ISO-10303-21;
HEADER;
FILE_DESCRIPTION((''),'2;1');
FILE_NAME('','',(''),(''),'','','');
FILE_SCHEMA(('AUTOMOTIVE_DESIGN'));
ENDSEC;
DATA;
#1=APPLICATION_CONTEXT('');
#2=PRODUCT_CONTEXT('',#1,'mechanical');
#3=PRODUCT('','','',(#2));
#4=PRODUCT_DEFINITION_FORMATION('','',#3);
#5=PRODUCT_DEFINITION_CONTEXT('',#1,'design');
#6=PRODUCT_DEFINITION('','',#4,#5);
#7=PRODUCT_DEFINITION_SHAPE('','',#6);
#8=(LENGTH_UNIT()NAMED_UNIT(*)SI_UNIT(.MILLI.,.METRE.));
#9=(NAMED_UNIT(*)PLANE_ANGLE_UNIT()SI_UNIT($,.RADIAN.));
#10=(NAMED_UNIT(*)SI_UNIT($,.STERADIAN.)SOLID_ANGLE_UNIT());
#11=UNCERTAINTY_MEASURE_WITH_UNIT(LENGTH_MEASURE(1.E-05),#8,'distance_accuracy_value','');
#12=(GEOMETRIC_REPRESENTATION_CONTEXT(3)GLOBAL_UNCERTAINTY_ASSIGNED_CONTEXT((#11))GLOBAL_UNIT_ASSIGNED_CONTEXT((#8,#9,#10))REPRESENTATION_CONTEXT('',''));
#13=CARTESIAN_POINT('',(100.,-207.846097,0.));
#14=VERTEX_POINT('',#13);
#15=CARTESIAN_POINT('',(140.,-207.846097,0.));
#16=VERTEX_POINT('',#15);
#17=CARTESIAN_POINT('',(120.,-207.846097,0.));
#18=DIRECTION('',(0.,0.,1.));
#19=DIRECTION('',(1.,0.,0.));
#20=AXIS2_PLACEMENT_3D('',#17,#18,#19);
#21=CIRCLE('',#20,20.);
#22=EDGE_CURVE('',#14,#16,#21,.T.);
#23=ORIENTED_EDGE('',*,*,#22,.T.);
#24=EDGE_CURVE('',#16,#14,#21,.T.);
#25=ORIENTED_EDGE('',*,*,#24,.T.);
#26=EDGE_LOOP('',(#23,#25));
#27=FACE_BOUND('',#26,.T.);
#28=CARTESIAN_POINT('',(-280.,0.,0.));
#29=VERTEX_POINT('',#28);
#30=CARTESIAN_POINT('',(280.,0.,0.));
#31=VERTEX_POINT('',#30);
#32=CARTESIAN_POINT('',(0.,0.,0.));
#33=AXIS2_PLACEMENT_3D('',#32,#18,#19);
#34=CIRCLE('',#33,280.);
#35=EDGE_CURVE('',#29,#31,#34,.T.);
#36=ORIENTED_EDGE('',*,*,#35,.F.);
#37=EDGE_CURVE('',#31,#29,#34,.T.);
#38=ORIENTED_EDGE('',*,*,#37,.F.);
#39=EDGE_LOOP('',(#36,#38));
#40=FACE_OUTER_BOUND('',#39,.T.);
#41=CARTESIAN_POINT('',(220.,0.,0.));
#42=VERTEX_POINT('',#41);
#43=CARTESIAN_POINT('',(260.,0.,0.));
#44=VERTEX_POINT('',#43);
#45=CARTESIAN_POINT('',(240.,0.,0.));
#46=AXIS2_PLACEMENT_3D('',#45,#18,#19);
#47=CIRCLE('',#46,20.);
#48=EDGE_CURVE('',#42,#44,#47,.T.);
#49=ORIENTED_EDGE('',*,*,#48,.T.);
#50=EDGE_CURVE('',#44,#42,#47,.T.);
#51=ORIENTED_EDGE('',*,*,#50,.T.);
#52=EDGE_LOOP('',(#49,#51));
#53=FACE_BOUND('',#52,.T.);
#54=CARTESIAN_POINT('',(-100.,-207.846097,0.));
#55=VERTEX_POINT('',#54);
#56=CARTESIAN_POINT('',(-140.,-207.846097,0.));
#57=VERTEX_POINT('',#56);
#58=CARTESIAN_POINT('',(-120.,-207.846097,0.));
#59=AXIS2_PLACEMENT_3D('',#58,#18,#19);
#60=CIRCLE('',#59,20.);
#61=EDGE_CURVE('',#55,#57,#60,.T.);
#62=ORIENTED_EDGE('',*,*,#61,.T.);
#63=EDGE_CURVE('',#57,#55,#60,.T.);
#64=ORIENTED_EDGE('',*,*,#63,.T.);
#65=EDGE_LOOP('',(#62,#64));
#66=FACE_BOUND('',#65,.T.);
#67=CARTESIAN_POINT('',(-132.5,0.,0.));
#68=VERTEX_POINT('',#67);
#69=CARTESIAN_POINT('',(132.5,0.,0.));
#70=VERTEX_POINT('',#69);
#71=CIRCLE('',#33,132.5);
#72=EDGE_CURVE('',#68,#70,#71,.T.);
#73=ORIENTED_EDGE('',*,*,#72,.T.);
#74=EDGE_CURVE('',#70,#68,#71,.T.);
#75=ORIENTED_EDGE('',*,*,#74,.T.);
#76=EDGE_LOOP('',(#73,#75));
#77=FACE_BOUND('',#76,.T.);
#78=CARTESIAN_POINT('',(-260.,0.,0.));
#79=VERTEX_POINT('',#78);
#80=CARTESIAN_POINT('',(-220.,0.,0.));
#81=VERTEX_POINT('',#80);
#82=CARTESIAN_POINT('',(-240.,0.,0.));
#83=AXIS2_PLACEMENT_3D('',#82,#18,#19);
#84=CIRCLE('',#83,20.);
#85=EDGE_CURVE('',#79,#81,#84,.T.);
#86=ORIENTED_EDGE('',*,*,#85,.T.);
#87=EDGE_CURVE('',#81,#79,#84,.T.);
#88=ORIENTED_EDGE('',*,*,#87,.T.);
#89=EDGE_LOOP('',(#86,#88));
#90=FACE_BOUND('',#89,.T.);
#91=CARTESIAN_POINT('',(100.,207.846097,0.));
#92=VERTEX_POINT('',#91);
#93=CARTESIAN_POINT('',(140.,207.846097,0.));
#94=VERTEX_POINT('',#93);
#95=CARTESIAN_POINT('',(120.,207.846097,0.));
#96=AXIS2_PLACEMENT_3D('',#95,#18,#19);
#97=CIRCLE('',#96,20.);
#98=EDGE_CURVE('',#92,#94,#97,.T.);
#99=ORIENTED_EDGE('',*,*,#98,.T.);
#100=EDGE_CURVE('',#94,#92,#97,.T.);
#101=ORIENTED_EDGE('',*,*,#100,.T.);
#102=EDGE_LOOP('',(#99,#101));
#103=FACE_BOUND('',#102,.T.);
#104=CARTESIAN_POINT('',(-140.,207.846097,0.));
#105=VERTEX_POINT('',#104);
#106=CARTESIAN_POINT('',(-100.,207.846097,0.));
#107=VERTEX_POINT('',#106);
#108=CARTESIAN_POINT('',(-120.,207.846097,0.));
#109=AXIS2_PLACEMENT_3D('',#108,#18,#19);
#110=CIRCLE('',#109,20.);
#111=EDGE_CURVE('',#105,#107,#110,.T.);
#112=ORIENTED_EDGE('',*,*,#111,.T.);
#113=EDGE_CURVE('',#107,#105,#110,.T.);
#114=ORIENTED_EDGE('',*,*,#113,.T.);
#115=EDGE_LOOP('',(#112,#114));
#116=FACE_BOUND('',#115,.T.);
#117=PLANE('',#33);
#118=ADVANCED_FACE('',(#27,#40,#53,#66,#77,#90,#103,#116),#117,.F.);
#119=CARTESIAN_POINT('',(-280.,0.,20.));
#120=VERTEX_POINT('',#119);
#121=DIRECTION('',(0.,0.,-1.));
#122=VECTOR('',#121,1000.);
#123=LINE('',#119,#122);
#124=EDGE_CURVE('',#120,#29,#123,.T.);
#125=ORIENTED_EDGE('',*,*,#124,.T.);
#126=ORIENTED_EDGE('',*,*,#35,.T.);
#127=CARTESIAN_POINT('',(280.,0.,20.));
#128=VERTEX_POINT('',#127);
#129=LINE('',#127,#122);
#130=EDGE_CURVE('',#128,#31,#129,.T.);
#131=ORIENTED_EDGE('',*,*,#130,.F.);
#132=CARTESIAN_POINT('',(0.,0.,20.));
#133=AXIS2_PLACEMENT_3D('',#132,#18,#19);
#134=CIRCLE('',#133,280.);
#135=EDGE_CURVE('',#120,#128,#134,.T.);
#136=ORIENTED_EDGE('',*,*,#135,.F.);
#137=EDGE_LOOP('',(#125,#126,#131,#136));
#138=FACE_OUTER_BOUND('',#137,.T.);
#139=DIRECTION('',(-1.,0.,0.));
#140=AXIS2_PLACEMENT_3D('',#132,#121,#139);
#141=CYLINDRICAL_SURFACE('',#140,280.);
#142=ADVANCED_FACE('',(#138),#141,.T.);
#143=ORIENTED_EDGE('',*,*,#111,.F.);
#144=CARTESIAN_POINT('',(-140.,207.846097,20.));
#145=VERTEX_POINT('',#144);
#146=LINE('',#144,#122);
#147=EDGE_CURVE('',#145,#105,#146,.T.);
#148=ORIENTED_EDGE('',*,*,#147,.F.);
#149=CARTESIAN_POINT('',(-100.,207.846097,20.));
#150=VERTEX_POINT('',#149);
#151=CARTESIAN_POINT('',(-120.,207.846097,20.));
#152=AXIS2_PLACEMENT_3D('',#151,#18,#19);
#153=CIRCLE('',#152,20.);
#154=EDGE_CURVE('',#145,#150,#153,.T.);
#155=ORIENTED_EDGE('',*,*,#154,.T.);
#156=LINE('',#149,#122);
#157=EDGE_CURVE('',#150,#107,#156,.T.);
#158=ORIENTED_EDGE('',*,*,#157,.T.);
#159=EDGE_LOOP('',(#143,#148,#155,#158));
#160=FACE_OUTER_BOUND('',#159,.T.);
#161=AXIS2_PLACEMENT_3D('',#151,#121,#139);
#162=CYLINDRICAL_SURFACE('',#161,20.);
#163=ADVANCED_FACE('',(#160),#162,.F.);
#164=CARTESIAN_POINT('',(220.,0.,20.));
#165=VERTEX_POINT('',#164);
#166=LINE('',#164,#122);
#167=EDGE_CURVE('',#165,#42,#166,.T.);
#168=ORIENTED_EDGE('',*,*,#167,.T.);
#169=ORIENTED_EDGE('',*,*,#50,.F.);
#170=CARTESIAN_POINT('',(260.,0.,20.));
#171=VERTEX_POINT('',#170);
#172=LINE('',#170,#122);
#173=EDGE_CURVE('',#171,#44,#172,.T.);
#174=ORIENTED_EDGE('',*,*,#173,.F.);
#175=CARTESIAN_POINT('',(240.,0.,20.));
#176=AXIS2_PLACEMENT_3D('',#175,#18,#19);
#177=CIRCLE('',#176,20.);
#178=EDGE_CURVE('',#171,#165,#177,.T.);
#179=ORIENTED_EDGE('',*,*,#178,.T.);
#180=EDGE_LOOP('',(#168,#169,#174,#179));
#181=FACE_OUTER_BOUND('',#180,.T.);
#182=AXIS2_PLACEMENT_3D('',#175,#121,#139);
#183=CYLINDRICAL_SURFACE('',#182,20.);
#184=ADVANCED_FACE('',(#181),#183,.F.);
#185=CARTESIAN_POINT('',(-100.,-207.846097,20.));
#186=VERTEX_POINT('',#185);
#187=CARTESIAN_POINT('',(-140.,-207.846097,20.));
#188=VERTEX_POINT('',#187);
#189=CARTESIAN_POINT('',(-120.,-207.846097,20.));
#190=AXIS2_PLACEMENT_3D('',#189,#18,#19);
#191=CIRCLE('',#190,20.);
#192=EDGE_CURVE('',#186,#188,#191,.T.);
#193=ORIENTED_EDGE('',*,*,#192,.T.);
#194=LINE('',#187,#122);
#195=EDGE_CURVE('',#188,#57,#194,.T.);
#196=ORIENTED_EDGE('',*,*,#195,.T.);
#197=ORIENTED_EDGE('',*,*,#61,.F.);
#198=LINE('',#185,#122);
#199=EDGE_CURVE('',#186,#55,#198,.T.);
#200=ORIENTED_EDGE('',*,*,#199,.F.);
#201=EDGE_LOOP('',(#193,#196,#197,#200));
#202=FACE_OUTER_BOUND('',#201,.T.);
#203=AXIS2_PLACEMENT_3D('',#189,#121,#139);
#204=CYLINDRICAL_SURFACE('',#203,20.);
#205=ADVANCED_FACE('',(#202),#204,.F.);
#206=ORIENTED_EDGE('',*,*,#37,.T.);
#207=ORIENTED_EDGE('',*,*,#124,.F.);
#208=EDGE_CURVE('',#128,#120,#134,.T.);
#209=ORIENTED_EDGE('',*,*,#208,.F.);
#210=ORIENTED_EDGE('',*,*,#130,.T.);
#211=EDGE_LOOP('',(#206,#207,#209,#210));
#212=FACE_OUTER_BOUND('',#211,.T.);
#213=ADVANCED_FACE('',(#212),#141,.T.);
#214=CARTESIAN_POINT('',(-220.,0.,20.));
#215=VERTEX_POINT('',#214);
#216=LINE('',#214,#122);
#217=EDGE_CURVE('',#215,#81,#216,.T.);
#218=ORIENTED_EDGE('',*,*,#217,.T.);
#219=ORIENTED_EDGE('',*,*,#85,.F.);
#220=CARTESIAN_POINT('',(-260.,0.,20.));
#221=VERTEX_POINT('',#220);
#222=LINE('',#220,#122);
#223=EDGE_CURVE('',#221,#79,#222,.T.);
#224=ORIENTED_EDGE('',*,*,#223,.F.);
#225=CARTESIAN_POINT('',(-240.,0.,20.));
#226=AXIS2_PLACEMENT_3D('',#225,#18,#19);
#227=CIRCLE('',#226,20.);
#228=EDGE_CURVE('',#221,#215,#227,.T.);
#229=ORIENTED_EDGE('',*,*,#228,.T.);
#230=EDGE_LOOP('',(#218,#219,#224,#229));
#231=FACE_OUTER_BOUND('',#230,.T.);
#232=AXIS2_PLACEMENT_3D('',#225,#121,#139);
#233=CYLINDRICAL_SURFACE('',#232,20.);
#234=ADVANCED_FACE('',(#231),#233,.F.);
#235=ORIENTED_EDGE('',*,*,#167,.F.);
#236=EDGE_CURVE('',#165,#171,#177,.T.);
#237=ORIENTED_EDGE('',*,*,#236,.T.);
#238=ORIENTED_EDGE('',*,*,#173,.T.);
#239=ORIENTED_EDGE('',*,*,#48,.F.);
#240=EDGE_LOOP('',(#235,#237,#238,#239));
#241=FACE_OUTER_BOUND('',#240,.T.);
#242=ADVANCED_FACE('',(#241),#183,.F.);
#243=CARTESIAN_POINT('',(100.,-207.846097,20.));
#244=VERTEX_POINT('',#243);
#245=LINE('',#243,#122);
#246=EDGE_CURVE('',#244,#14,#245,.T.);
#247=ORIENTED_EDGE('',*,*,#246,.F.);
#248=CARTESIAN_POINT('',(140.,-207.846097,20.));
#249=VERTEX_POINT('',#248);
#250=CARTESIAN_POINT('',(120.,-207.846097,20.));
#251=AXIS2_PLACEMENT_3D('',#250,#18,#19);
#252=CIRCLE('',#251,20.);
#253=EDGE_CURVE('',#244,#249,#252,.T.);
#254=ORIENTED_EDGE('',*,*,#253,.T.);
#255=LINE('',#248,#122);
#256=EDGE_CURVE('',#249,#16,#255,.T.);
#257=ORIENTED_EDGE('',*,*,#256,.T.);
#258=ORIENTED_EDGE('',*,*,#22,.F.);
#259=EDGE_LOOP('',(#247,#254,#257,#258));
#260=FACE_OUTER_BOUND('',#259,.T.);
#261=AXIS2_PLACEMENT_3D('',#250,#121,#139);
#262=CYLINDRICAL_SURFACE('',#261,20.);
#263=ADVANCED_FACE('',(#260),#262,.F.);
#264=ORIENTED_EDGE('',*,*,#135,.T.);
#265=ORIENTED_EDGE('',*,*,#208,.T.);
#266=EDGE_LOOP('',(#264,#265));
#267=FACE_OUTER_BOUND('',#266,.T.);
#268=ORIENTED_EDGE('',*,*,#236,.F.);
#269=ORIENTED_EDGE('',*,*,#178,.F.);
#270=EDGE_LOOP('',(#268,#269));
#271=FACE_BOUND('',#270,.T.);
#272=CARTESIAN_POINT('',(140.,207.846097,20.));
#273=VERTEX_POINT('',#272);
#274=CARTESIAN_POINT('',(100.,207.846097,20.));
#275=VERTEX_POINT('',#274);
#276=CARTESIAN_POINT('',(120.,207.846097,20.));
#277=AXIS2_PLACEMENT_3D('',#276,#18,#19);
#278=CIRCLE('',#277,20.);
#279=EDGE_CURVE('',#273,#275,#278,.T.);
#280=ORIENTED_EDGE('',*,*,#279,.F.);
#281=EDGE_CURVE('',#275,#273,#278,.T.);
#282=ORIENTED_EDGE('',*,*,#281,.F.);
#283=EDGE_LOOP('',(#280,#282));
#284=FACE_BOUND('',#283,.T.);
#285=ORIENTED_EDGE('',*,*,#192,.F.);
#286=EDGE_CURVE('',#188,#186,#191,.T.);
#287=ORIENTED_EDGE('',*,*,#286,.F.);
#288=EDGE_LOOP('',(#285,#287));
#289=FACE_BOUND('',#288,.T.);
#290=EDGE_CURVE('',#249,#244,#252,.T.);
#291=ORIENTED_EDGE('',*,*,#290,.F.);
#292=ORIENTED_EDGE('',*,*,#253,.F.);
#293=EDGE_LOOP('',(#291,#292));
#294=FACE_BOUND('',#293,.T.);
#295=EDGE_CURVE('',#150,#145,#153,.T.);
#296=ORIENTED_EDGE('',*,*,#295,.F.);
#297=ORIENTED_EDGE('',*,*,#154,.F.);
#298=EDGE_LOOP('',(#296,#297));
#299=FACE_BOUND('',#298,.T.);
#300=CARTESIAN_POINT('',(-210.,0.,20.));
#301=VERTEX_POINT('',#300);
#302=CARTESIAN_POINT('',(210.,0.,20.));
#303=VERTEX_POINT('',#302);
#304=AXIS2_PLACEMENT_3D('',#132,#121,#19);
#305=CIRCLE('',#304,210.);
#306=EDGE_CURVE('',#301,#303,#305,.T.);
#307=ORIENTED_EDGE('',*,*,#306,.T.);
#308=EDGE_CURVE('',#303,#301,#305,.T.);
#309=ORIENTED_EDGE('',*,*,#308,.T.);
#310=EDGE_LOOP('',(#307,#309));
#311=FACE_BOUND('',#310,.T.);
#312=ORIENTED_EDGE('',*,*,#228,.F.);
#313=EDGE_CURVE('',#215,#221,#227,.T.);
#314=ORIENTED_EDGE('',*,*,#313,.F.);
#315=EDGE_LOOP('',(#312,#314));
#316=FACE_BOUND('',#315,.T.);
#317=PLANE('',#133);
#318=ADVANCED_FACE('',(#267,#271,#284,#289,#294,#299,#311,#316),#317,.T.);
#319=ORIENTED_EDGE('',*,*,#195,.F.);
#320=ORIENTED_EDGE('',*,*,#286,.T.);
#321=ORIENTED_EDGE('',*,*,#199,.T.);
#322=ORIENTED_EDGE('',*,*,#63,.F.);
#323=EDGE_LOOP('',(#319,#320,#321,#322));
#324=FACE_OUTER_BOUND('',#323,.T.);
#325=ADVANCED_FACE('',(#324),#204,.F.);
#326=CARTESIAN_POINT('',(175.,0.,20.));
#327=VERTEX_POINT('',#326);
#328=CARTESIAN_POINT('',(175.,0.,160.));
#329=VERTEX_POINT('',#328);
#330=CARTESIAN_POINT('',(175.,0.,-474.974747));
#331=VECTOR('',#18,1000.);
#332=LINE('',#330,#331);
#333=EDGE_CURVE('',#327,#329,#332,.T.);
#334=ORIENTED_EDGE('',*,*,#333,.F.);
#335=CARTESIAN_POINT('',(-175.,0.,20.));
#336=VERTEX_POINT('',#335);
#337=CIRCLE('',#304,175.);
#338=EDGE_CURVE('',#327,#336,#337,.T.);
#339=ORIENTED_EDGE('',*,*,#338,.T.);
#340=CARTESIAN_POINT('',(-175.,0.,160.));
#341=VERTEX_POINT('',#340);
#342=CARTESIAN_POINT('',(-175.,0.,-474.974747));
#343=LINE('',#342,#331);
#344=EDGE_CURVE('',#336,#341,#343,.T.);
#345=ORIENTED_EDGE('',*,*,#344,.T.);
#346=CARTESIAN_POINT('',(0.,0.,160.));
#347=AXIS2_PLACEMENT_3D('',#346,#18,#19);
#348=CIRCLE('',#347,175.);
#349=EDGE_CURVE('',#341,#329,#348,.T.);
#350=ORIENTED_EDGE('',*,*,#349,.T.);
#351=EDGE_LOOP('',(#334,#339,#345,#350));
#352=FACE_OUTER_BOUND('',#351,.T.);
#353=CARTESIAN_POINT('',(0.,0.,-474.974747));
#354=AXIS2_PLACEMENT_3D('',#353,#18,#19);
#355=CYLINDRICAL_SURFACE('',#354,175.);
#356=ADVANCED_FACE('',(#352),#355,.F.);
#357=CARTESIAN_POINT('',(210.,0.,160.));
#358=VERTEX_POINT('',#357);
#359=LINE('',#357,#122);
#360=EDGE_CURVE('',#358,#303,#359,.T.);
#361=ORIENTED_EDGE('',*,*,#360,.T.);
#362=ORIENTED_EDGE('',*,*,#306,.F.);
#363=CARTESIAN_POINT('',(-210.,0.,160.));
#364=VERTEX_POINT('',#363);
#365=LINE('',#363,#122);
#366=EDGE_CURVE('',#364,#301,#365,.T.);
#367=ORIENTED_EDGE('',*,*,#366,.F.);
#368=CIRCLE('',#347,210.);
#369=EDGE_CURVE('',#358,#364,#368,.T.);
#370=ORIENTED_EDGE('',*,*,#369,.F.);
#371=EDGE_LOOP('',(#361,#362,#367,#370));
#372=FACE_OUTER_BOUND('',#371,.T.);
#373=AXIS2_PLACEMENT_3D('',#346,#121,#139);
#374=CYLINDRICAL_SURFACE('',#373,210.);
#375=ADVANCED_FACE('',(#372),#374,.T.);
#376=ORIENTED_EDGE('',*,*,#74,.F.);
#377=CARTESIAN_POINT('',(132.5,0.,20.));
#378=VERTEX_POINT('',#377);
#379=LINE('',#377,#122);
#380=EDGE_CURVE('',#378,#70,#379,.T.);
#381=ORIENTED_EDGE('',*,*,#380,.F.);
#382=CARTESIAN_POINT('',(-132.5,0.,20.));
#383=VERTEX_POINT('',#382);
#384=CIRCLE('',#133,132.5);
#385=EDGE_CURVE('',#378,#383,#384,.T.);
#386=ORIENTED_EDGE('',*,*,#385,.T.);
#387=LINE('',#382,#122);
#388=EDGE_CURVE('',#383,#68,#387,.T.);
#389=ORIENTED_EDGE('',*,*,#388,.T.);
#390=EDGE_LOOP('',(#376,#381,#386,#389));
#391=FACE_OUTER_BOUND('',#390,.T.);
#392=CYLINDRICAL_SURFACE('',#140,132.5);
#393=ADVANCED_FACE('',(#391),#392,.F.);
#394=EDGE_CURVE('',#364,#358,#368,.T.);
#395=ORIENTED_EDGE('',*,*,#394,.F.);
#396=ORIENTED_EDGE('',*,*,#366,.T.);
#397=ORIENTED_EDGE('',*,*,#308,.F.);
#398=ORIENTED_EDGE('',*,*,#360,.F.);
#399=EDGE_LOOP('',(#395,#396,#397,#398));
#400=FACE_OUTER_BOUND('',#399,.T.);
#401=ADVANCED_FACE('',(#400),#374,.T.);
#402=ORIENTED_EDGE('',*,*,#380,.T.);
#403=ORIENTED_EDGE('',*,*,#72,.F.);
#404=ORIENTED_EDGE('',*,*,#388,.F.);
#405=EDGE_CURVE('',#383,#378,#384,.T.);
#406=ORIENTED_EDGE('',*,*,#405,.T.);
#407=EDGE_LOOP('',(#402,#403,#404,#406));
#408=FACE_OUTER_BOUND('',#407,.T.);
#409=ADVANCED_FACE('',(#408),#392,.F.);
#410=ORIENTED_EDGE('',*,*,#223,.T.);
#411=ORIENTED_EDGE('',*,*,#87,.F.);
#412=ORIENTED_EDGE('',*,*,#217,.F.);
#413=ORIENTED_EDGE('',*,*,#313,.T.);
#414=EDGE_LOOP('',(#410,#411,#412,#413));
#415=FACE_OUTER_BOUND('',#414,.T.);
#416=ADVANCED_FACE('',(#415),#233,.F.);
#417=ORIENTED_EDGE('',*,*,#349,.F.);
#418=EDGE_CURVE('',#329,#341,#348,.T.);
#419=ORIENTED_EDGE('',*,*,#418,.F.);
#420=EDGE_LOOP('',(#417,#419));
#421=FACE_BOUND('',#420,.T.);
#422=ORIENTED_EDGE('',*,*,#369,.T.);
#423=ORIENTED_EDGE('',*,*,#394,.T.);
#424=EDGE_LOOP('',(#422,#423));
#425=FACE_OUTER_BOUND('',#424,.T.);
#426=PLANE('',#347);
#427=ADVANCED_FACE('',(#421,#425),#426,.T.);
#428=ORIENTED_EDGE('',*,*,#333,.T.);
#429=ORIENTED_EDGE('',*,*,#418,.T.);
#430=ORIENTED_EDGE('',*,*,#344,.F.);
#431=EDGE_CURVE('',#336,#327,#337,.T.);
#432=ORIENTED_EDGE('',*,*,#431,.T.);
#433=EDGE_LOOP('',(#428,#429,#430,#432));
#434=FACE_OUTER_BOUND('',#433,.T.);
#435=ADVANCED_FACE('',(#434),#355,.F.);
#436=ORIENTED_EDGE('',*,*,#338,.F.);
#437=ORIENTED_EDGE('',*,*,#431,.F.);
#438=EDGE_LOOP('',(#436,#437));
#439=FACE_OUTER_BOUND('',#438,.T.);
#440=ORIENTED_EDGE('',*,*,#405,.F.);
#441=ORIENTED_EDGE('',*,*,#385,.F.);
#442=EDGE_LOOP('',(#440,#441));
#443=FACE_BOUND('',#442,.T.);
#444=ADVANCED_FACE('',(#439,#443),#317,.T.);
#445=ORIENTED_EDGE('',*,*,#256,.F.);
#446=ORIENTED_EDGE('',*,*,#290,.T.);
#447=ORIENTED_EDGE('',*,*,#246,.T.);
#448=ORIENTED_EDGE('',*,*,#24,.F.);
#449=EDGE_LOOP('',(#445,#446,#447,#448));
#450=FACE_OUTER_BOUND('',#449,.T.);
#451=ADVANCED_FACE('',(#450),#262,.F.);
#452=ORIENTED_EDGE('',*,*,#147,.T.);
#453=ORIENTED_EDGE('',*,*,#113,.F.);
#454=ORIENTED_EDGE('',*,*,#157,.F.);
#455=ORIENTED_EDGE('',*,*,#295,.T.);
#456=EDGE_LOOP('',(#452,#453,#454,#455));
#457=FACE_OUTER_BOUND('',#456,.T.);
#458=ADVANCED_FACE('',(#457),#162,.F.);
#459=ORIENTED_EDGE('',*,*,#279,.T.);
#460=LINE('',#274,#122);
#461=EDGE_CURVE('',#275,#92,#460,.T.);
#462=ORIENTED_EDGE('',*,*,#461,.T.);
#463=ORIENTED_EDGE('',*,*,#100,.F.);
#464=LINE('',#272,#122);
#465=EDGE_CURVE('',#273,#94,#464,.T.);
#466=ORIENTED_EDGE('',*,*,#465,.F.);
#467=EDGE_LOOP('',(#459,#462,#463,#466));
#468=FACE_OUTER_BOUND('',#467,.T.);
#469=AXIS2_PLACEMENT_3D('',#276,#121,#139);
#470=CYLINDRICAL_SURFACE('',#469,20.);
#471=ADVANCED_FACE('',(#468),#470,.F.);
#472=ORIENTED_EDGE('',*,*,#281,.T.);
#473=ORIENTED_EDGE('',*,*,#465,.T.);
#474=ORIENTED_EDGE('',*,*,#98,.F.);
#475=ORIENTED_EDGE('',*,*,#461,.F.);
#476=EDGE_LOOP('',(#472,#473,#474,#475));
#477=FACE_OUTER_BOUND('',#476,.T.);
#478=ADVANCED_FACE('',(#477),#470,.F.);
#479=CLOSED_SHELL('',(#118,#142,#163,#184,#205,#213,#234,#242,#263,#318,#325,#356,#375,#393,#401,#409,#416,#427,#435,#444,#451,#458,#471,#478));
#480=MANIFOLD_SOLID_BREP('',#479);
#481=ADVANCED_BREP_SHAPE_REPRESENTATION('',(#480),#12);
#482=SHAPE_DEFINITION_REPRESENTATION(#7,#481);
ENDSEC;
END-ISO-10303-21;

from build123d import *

# Parameters (mm, degrees)
SKETCH_1_R          = 280
EXTRUDE_1_DEPTH     = 20
SKETCH_2_R          = 210
EXTRUDE_2_DEPTH     = 160
SKETCH_3_R          = 175
CUT_EXTRUDE_1_DEPTH = 140
SKETCH_4_R          = 20
CUT_EXTRUDE_3_DEPTH = 20
SKETCH_5_R          = 132.5
CUT_EXTRUDE_4_DEPTH = 20


with BuildPart() as part:
    # 草图1 → 凸台-拉伸1 (new body)
    with BuildSketch(Plane.XY):
        Circle(SKETCH_1_R)
    extrude(amount=EXTRUDE_1_DEPTH)

    # 草图2 → 凸台-拉伸2 (add)
    with BuildSketch(Plane.XY):
        Circle(SKETCH_2_R)
    extrude(amount=EXTRUDE_2_DEPTH)

    # 草图3 → 切除-拉伸1 (cut)
    with BuildSketch(Plane.XY.offset(160)):
        Circle(SKETCH_3_R)
    extrude(amount=-CUT_EXTRUDE_1_DEPTH, mode=Mode.SUBTRACT)

    # 草图4 → 切除-拉伸3 (cut)
    with BuildSketch(Plane.XY):
        with Locations((240, 0)):
            Circle(SKETCH_4_R)
        with Locations((-240, 0)):
            Circle(SKETCH_4_R)
        with Locations((-120, 207.846096908)):
            Circle(SKETCH_4_R)
        with Locations((120, 207.846096908)):
            Circle(SKETCH_4_R)
        with Locations((-120, -207.846096908)):
            Circle(SKETCH_4_R)
        with Locations((120, -207.846096908)):
            Circle(SKETCH_4_R)
    extrude(amount=CUT_EXTRUDE_3_DEPTH, mode=Mode.SUBTRACT)

    # 草图5 → 切除-拉伸4 (cut)
    with BuildSketch(Plane.XY):
        Circle(SKETCH_5_R)
    extrude(amount=CUT_EXTRUDE_4_DEPTH, mode=Mode.SUBTRACT)


solid = part.part
